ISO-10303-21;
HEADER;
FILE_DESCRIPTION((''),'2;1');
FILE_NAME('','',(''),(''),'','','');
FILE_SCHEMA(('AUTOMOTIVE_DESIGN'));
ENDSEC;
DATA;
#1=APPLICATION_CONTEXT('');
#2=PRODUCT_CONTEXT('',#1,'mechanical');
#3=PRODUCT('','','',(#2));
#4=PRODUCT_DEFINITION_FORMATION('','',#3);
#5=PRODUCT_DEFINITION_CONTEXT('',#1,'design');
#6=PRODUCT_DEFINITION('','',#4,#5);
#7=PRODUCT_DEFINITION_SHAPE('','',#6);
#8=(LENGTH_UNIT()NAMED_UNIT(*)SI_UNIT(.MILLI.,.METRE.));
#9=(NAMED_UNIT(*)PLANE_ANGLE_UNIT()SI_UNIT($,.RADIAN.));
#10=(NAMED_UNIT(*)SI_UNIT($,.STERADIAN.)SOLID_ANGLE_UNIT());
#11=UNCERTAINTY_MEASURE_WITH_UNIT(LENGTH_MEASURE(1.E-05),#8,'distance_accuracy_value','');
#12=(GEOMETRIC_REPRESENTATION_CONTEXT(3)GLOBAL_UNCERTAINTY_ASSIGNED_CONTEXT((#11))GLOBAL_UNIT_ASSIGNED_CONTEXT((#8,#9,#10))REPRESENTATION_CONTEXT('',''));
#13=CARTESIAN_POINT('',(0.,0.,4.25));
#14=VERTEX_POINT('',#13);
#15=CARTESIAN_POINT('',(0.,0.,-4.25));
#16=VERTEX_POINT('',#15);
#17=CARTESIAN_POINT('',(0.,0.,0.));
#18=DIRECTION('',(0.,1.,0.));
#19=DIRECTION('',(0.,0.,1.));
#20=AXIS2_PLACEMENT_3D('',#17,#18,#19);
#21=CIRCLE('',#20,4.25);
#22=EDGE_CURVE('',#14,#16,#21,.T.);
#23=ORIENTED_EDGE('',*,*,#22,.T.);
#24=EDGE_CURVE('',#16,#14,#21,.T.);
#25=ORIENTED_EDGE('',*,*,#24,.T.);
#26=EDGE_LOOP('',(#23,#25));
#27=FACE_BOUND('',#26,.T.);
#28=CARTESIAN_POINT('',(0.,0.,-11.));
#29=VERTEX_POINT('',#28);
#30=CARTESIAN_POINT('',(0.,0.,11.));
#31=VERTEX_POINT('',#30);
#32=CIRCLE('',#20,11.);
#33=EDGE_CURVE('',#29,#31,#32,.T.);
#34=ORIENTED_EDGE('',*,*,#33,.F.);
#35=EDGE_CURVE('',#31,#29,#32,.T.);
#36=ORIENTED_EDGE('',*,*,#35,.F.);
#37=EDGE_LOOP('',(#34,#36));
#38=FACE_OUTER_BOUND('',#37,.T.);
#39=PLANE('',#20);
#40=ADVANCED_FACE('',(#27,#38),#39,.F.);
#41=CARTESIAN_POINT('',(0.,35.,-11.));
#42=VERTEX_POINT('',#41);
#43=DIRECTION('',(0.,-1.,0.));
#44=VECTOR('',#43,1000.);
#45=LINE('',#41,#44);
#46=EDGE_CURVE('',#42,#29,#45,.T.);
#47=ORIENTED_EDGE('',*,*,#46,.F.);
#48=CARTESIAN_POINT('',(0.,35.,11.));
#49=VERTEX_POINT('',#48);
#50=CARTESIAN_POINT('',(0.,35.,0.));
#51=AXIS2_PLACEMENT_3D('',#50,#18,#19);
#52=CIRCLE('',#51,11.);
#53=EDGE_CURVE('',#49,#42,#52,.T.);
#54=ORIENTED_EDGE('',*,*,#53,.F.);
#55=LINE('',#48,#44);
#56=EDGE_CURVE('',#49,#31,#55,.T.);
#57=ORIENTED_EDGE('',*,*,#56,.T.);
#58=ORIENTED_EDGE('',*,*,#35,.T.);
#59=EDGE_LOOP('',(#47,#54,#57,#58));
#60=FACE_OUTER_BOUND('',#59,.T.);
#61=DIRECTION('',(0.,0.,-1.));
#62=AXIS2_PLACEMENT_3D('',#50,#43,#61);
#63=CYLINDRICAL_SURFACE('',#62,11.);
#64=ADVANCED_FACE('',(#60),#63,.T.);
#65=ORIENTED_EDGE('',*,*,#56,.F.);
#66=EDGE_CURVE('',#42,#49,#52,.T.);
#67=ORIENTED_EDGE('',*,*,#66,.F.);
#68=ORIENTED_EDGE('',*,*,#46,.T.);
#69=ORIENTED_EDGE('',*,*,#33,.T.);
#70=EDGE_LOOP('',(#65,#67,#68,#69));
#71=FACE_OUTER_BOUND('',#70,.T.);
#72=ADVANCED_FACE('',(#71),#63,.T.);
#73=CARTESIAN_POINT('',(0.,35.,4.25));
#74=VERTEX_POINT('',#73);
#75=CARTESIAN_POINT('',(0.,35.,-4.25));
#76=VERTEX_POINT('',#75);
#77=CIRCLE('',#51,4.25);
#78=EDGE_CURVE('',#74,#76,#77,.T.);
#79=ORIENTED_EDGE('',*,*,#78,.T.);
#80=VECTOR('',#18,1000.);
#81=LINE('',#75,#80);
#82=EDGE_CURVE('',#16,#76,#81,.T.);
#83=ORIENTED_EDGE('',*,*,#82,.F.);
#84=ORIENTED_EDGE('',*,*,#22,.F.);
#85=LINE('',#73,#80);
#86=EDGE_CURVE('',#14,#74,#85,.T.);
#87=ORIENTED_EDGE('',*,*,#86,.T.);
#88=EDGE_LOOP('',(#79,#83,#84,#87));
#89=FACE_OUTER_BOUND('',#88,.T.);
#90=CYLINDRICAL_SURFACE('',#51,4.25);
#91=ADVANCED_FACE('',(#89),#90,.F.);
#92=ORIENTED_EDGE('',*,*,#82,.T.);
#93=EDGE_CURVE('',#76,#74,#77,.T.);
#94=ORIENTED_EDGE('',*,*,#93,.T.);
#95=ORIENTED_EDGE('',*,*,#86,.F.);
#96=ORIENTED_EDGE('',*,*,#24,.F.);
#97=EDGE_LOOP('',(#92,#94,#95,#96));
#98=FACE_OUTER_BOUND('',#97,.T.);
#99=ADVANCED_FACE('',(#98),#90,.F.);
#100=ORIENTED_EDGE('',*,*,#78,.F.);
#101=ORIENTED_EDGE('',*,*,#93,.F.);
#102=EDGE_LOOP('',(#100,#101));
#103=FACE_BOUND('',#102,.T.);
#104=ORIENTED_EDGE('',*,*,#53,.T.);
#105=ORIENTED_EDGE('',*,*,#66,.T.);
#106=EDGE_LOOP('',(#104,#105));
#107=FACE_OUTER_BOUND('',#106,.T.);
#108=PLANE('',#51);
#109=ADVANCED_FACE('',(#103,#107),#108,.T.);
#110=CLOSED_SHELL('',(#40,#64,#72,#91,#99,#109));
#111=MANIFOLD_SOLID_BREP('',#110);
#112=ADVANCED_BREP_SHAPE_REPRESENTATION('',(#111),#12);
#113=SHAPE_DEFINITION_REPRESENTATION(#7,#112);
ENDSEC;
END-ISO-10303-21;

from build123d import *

# Parameters (mm, degrees)
SKETCH1_R           = 11
BOSS_EXTRUDE1_DEPTH = 35
M10_TAPPED_HOLE1_D  = 8.5


with BuildPart() as part:
    # Sketch1 → Boss-Extrude1 (new body)
    with BuildSketch(Plane(origin=(0, 0, 0), x_dir=(1, 0, 0), z_dir=(0, 1, 0))):
        with Locations(Location((0, 0, 0), (0, 0, 270))):
            Circle(SKETCH1_R)
    extrude(amount=BOSS_EXTRUDE1_DEPTH)

    # M10 Tapped Hole1 (through all)
    with Locations(Plane(origin=(0, 35, 0), x_dir=(1, 0, 0), z_dir=(0, 1, 0))):
        with Locations((0, 0)):
            Hole(M10_TAPPED_HOLE1_D / 2)


solid = part.part
